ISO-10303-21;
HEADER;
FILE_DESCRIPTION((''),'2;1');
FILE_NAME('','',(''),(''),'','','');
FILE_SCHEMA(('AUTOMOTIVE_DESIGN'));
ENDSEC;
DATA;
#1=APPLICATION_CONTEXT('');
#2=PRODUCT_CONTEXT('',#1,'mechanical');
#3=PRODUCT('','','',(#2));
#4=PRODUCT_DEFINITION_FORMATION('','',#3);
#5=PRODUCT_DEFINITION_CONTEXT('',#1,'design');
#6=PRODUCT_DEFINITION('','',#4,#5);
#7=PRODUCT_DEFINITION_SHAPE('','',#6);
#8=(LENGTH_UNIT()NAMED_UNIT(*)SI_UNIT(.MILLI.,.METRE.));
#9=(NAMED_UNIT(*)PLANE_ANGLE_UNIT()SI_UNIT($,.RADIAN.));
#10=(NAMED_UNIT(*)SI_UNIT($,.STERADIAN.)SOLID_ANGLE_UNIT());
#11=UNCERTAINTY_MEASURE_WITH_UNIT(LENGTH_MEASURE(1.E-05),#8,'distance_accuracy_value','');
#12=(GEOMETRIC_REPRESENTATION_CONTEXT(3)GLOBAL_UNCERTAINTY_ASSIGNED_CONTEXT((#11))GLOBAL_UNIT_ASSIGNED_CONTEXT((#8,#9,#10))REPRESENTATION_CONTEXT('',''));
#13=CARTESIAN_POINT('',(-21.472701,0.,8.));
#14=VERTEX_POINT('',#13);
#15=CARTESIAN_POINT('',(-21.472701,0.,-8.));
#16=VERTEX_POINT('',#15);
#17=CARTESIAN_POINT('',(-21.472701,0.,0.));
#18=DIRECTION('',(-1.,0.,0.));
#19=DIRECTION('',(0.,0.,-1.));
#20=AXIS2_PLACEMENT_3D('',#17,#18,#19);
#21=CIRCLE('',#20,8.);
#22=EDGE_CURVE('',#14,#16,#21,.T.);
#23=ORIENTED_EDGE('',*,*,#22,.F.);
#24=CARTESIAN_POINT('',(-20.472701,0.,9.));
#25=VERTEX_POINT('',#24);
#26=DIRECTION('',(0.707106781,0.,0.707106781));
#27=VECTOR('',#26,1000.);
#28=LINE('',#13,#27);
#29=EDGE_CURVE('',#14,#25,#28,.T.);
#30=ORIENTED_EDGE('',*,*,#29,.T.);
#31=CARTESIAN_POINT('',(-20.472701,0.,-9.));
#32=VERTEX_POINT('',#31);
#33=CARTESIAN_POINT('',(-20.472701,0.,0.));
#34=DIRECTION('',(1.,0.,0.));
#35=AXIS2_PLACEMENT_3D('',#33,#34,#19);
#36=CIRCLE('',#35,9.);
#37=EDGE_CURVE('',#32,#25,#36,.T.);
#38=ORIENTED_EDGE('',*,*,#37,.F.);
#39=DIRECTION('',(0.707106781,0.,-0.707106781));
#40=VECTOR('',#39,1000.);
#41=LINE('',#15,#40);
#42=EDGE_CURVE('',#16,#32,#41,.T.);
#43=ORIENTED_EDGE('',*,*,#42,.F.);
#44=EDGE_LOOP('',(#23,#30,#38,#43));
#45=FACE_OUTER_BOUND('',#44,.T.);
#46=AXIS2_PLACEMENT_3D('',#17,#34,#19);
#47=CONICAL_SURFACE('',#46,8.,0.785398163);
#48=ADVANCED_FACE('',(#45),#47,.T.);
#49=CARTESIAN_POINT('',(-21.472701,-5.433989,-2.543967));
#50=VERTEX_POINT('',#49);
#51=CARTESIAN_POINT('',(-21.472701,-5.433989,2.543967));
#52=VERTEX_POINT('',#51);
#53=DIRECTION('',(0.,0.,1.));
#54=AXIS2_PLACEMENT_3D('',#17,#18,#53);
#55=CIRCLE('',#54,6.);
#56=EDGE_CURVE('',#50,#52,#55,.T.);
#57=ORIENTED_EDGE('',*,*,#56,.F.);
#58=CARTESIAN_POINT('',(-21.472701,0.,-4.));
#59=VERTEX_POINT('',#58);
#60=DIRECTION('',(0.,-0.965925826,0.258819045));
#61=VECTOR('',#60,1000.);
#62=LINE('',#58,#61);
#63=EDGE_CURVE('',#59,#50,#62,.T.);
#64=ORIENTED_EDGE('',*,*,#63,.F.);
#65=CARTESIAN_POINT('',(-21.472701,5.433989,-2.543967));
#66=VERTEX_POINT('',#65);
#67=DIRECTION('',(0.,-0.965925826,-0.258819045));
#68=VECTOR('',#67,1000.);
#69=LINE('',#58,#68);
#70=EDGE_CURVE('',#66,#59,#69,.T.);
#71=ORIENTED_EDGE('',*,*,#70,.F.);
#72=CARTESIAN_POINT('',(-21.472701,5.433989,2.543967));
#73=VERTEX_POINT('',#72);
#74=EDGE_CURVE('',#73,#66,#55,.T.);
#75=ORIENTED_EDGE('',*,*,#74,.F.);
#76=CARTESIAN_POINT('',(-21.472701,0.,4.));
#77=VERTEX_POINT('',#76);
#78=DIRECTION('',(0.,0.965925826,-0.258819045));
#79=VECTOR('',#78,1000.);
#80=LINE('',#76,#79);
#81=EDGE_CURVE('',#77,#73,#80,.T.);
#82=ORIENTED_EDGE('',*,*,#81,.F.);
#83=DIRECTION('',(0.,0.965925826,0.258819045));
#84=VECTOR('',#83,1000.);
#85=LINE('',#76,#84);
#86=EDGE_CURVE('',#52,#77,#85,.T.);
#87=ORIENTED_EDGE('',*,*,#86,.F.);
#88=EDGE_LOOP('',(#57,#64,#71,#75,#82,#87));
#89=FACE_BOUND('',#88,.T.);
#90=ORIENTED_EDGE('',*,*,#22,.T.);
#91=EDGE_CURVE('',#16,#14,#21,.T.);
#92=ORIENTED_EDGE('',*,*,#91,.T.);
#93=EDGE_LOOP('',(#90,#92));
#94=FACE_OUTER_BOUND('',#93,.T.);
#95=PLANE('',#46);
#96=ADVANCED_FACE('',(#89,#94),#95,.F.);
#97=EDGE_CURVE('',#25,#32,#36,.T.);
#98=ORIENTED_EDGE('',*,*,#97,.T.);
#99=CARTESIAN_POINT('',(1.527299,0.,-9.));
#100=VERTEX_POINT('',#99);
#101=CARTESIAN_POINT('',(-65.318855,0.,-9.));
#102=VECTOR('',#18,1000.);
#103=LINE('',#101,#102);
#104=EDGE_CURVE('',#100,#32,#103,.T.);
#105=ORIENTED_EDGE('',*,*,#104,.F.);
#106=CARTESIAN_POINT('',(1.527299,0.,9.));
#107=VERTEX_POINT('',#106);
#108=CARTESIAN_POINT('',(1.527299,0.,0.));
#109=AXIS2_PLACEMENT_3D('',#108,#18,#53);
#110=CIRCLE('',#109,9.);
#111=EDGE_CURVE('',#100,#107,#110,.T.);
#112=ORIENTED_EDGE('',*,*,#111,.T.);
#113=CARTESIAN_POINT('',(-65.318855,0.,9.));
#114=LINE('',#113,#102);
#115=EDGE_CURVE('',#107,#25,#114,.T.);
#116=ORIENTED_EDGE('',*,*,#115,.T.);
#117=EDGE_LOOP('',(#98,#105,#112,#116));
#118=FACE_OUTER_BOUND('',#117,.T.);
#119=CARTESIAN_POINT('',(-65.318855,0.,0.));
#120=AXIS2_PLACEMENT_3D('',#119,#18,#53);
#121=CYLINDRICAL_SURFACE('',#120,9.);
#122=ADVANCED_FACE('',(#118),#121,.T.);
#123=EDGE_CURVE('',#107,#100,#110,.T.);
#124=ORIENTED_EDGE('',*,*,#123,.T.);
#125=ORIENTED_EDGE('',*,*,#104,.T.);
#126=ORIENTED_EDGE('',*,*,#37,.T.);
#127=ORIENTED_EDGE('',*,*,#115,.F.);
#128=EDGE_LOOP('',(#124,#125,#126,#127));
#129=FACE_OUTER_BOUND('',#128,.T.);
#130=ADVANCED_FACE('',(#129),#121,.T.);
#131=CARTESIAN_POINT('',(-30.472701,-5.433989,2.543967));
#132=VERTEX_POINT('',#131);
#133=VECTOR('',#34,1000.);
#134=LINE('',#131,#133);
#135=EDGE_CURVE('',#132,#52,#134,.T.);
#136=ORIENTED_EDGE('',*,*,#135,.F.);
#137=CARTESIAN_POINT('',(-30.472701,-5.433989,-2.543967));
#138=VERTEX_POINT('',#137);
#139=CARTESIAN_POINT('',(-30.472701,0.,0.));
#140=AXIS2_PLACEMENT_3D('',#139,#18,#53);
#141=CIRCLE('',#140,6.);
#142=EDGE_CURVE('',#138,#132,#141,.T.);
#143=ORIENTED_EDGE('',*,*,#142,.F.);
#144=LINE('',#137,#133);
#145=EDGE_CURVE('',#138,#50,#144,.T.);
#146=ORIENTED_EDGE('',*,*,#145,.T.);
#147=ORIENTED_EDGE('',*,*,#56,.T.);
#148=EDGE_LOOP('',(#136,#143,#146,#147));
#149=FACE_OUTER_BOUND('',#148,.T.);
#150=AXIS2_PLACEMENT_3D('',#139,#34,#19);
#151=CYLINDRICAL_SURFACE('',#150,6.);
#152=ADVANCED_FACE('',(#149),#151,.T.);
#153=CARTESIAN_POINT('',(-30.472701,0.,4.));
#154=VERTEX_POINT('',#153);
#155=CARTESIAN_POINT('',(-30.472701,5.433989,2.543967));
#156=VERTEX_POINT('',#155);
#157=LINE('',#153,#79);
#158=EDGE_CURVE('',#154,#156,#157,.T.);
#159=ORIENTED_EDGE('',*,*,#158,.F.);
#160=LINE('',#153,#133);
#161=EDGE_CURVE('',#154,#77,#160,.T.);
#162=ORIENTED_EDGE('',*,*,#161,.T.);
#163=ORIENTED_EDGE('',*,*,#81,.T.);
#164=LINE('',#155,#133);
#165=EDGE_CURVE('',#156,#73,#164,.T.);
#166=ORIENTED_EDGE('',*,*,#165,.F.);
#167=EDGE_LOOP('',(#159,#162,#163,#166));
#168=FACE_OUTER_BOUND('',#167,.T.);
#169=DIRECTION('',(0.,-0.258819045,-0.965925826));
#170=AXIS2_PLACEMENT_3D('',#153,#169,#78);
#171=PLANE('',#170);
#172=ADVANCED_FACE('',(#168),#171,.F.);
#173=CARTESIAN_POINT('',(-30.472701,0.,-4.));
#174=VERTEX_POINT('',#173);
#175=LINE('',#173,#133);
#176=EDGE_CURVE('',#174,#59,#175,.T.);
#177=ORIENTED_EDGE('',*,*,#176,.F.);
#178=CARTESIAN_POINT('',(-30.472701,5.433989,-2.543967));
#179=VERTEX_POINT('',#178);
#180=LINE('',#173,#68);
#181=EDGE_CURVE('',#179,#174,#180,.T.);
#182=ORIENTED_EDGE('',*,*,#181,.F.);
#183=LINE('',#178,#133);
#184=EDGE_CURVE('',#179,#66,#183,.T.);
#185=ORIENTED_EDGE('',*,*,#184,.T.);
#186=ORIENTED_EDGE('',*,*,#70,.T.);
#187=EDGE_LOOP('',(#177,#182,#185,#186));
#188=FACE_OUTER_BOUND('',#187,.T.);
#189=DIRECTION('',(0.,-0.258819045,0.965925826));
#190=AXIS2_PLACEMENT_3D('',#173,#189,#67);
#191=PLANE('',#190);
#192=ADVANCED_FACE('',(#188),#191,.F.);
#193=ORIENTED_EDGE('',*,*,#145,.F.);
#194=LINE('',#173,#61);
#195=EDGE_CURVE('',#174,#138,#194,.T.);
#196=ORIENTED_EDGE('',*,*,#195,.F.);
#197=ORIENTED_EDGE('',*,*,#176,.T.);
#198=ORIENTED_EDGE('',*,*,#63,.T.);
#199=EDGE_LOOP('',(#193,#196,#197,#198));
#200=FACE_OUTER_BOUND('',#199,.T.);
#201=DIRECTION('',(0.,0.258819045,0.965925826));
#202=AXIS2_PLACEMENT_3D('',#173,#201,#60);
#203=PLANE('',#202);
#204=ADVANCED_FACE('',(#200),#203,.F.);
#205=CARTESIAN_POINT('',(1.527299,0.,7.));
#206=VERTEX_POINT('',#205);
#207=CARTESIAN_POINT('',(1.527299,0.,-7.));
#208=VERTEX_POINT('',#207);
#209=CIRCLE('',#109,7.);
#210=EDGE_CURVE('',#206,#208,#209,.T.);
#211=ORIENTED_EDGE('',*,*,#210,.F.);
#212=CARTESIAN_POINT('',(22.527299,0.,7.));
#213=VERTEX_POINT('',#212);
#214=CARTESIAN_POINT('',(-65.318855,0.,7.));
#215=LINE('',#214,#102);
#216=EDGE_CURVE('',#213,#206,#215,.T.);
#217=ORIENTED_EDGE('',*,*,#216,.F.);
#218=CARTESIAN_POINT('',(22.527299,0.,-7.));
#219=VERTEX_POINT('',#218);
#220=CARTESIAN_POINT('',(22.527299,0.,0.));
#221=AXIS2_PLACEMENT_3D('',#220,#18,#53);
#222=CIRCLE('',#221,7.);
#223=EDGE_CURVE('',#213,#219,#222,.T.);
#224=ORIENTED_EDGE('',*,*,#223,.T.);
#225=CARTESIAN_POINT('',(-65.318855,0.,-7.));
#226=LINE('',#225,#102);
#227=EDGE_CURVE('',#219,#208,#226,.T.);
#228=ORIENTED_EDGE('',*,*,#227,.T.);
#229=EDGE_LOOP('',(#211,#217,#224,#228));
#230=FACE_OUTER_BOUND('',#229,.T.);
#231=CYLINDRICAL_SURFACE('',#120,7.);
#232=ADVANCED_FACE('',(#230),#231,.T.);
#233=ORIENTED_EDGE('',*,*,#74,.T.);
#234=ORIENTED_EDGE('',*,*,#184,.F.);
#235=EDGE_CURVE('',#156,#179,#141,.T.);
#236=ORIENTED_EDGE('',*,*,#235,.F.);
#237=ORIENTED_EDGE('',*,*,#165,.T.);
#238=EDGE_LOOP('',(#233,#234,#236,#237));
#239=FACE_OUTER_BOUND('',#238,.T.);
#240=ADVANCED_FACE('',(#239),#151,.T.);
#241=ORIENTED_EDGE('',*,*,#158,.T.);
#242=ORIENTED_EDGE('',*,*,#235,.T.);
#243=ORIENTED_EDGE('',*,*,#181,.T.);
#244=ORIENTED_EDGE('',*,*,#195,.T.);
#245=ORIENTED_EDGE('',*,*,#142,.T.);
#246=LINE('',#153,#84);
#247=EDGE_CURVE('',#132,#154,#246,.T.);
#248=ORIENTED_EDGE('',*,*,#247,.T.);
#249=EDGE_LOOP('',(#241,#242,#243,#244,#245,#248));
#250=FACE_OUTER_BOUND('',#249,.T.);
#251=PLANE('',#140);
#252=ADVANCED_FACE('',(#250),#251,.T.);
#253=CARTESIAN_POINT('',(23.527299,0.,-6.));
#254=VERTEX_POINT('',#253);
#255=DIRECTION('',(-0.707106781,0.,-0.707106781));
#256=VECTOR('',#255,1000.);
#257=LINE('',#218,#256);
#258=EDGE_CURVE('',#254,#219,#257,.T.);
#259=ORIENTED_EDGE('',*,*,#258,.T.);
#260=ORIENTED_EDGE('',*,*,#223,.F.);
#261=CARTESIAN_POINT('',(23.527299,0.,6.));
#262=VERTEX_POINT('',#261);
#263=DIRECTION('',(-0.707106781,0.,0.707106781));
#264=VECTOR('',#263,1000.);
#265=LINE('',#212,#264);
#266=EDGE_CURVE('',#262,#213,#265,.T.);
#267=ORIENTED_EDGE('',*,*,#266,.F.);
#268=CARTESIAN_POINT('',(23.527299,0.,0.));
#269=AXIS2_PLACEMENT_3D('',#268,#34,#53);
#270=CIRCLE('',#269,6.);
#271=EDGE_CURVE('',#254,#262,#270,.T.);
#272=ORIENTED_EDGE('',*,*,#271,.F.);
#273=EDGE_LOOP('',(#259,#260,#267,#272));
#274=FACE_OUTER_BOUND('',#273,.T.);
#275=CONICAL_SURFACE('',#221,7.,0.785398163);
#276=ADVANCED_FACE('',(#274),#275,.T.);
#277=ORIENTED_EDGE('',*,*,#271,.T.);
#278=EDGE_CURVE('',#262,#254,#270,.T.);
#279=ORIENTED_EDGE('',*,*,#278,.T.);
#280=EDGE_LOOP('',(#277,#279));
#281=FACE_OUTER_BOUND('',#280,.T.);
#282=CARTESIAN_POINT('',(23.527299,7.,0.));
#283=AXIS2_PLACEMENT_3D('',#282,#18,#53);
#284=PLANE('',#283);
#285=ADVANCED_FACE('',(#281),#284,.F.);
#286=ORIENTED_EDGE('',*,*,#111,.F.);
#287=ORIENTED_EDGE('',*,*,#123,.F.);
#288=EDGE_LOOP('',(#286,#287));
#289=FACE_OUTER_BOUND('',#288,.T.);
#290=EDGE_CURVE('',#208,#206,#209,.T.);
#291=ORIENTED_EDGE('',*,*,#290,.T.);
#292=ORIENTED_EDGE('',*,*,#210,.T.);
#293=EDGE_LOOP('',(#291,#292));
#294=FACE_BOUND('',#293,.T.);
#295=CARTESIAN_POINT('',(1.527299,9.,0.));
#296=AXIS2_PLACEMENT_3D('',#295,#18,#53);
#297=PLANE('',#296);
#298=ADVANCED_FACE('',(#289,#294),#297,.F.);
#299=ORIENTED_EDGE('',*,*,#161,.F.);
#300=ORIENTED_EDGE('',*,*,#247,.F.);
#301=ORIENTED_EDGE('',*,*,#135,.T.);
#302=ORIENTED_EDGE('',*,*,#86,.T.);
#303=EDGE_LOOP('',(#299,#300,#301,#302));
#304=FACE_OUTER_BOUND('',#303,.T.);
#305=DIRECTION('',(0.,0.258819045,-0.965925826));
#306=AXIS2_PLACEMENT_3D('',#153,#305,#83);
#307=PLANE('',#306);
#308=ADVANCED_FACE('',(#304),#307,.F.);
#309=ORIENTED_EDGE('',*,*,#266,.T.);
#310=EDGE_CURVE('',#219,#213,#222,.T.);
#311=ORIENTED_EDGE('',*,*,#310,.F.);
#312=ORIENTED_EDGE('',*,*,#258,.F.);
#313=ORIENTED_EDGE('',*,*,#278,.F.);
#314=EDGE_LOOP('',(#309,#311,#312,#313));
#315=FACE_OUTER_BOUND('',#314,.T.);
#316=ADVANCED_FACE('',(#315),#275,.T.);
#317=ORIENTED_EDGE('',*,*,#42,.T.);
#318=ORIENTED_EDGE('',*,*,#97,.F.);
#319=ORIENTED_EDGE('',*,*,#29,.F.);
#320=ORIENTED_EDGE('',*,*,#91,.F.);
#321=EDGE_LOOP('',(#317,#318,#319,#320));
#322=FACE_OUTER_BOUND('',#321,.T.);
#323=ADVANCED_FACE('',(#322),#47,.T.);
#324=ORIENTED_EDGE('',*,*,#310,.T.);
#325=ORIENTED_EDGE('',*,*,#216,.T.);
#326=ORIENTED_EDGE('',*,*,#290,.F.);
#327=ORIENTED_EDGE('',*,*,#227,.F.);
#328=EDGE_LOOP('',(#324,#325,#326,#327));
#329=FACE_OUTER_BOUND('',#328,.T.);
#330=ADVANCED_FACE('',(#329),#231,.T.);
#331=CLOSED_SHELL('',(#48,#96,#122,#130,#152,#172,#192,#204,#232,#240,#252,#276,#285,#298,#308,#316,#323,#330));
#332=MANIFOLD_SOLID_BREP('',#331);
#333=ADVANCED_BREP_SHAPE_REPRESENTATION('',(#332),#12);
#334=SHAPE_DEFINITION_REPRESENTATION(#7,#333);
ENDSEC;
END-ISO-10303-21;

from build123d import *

# Parameters (mm, degrees)
CHAMFER1_SIZE       = 1
CHAMFER2_SIZE       = 1
BOSS_EXTRUDE1_DEPTH = 9


with BuildPart() as part:
    # Sketch1 → Revolve1 (revolve)
    with BuildSketch(Plane.XY, mode=Mode.PRIVATE) as revolve1_sk:
        Polygon((-21.47270101, 0), (-21.47270101, 9), (1.52729899, 9), (1.52729899, 7), (23.52729899, 7), (23.52729899, 0), align=None)
    revolve(revolve1_sk.sketch.rotate(Axis((-65.318854856, 0, 0), (1, 0, 0)), 90), axis=Axis((-65.318854856, 0, 0), (1, 0, 0)))

    # Chamfer1
    chamfer1_edges = [part.edges().sort_by_distance(p)[0] for p in [
        (23.52729899, 0, -7),
    ]]
    chamfer(chamfer1_edges, length=CHAMFER1_SIZE)

    # Chamfer2
    chamfer2_edges = [part.edges().sort_by_distance(p)[0] for p in [
        (-21.47270101, 0, -9),
    ]]
    chamfer(chamfer2_edges, length=CHAMFER2_SIZE)

    # Sketch3 → Boss-Extrude1 (add)
    with BuildSketch(Plane.ZY.offset(21.47270101)):
        with BuildLine():
            Line((4, 0), (2.543967169, 5.433988502))
            ThreePointArc((2.543967169, 5.433988502), (0, 6), (-2.543967169, 5.433988502))
            Line((-2.543967169, 5.433988502), (-4, 0))
            Line((-4, 0), (-2.543967169, -5.433988502))
            ThreePointArc((-2.543967169, -5.433988502), (0, -6), (2.543967169, -5.433988502))
            Line((2.543967169, -5.433988502), (4, 0))
        make_face()
    extrude(amount=BOSS_EXTRUDE1_DEPTH)


solid = part.part
